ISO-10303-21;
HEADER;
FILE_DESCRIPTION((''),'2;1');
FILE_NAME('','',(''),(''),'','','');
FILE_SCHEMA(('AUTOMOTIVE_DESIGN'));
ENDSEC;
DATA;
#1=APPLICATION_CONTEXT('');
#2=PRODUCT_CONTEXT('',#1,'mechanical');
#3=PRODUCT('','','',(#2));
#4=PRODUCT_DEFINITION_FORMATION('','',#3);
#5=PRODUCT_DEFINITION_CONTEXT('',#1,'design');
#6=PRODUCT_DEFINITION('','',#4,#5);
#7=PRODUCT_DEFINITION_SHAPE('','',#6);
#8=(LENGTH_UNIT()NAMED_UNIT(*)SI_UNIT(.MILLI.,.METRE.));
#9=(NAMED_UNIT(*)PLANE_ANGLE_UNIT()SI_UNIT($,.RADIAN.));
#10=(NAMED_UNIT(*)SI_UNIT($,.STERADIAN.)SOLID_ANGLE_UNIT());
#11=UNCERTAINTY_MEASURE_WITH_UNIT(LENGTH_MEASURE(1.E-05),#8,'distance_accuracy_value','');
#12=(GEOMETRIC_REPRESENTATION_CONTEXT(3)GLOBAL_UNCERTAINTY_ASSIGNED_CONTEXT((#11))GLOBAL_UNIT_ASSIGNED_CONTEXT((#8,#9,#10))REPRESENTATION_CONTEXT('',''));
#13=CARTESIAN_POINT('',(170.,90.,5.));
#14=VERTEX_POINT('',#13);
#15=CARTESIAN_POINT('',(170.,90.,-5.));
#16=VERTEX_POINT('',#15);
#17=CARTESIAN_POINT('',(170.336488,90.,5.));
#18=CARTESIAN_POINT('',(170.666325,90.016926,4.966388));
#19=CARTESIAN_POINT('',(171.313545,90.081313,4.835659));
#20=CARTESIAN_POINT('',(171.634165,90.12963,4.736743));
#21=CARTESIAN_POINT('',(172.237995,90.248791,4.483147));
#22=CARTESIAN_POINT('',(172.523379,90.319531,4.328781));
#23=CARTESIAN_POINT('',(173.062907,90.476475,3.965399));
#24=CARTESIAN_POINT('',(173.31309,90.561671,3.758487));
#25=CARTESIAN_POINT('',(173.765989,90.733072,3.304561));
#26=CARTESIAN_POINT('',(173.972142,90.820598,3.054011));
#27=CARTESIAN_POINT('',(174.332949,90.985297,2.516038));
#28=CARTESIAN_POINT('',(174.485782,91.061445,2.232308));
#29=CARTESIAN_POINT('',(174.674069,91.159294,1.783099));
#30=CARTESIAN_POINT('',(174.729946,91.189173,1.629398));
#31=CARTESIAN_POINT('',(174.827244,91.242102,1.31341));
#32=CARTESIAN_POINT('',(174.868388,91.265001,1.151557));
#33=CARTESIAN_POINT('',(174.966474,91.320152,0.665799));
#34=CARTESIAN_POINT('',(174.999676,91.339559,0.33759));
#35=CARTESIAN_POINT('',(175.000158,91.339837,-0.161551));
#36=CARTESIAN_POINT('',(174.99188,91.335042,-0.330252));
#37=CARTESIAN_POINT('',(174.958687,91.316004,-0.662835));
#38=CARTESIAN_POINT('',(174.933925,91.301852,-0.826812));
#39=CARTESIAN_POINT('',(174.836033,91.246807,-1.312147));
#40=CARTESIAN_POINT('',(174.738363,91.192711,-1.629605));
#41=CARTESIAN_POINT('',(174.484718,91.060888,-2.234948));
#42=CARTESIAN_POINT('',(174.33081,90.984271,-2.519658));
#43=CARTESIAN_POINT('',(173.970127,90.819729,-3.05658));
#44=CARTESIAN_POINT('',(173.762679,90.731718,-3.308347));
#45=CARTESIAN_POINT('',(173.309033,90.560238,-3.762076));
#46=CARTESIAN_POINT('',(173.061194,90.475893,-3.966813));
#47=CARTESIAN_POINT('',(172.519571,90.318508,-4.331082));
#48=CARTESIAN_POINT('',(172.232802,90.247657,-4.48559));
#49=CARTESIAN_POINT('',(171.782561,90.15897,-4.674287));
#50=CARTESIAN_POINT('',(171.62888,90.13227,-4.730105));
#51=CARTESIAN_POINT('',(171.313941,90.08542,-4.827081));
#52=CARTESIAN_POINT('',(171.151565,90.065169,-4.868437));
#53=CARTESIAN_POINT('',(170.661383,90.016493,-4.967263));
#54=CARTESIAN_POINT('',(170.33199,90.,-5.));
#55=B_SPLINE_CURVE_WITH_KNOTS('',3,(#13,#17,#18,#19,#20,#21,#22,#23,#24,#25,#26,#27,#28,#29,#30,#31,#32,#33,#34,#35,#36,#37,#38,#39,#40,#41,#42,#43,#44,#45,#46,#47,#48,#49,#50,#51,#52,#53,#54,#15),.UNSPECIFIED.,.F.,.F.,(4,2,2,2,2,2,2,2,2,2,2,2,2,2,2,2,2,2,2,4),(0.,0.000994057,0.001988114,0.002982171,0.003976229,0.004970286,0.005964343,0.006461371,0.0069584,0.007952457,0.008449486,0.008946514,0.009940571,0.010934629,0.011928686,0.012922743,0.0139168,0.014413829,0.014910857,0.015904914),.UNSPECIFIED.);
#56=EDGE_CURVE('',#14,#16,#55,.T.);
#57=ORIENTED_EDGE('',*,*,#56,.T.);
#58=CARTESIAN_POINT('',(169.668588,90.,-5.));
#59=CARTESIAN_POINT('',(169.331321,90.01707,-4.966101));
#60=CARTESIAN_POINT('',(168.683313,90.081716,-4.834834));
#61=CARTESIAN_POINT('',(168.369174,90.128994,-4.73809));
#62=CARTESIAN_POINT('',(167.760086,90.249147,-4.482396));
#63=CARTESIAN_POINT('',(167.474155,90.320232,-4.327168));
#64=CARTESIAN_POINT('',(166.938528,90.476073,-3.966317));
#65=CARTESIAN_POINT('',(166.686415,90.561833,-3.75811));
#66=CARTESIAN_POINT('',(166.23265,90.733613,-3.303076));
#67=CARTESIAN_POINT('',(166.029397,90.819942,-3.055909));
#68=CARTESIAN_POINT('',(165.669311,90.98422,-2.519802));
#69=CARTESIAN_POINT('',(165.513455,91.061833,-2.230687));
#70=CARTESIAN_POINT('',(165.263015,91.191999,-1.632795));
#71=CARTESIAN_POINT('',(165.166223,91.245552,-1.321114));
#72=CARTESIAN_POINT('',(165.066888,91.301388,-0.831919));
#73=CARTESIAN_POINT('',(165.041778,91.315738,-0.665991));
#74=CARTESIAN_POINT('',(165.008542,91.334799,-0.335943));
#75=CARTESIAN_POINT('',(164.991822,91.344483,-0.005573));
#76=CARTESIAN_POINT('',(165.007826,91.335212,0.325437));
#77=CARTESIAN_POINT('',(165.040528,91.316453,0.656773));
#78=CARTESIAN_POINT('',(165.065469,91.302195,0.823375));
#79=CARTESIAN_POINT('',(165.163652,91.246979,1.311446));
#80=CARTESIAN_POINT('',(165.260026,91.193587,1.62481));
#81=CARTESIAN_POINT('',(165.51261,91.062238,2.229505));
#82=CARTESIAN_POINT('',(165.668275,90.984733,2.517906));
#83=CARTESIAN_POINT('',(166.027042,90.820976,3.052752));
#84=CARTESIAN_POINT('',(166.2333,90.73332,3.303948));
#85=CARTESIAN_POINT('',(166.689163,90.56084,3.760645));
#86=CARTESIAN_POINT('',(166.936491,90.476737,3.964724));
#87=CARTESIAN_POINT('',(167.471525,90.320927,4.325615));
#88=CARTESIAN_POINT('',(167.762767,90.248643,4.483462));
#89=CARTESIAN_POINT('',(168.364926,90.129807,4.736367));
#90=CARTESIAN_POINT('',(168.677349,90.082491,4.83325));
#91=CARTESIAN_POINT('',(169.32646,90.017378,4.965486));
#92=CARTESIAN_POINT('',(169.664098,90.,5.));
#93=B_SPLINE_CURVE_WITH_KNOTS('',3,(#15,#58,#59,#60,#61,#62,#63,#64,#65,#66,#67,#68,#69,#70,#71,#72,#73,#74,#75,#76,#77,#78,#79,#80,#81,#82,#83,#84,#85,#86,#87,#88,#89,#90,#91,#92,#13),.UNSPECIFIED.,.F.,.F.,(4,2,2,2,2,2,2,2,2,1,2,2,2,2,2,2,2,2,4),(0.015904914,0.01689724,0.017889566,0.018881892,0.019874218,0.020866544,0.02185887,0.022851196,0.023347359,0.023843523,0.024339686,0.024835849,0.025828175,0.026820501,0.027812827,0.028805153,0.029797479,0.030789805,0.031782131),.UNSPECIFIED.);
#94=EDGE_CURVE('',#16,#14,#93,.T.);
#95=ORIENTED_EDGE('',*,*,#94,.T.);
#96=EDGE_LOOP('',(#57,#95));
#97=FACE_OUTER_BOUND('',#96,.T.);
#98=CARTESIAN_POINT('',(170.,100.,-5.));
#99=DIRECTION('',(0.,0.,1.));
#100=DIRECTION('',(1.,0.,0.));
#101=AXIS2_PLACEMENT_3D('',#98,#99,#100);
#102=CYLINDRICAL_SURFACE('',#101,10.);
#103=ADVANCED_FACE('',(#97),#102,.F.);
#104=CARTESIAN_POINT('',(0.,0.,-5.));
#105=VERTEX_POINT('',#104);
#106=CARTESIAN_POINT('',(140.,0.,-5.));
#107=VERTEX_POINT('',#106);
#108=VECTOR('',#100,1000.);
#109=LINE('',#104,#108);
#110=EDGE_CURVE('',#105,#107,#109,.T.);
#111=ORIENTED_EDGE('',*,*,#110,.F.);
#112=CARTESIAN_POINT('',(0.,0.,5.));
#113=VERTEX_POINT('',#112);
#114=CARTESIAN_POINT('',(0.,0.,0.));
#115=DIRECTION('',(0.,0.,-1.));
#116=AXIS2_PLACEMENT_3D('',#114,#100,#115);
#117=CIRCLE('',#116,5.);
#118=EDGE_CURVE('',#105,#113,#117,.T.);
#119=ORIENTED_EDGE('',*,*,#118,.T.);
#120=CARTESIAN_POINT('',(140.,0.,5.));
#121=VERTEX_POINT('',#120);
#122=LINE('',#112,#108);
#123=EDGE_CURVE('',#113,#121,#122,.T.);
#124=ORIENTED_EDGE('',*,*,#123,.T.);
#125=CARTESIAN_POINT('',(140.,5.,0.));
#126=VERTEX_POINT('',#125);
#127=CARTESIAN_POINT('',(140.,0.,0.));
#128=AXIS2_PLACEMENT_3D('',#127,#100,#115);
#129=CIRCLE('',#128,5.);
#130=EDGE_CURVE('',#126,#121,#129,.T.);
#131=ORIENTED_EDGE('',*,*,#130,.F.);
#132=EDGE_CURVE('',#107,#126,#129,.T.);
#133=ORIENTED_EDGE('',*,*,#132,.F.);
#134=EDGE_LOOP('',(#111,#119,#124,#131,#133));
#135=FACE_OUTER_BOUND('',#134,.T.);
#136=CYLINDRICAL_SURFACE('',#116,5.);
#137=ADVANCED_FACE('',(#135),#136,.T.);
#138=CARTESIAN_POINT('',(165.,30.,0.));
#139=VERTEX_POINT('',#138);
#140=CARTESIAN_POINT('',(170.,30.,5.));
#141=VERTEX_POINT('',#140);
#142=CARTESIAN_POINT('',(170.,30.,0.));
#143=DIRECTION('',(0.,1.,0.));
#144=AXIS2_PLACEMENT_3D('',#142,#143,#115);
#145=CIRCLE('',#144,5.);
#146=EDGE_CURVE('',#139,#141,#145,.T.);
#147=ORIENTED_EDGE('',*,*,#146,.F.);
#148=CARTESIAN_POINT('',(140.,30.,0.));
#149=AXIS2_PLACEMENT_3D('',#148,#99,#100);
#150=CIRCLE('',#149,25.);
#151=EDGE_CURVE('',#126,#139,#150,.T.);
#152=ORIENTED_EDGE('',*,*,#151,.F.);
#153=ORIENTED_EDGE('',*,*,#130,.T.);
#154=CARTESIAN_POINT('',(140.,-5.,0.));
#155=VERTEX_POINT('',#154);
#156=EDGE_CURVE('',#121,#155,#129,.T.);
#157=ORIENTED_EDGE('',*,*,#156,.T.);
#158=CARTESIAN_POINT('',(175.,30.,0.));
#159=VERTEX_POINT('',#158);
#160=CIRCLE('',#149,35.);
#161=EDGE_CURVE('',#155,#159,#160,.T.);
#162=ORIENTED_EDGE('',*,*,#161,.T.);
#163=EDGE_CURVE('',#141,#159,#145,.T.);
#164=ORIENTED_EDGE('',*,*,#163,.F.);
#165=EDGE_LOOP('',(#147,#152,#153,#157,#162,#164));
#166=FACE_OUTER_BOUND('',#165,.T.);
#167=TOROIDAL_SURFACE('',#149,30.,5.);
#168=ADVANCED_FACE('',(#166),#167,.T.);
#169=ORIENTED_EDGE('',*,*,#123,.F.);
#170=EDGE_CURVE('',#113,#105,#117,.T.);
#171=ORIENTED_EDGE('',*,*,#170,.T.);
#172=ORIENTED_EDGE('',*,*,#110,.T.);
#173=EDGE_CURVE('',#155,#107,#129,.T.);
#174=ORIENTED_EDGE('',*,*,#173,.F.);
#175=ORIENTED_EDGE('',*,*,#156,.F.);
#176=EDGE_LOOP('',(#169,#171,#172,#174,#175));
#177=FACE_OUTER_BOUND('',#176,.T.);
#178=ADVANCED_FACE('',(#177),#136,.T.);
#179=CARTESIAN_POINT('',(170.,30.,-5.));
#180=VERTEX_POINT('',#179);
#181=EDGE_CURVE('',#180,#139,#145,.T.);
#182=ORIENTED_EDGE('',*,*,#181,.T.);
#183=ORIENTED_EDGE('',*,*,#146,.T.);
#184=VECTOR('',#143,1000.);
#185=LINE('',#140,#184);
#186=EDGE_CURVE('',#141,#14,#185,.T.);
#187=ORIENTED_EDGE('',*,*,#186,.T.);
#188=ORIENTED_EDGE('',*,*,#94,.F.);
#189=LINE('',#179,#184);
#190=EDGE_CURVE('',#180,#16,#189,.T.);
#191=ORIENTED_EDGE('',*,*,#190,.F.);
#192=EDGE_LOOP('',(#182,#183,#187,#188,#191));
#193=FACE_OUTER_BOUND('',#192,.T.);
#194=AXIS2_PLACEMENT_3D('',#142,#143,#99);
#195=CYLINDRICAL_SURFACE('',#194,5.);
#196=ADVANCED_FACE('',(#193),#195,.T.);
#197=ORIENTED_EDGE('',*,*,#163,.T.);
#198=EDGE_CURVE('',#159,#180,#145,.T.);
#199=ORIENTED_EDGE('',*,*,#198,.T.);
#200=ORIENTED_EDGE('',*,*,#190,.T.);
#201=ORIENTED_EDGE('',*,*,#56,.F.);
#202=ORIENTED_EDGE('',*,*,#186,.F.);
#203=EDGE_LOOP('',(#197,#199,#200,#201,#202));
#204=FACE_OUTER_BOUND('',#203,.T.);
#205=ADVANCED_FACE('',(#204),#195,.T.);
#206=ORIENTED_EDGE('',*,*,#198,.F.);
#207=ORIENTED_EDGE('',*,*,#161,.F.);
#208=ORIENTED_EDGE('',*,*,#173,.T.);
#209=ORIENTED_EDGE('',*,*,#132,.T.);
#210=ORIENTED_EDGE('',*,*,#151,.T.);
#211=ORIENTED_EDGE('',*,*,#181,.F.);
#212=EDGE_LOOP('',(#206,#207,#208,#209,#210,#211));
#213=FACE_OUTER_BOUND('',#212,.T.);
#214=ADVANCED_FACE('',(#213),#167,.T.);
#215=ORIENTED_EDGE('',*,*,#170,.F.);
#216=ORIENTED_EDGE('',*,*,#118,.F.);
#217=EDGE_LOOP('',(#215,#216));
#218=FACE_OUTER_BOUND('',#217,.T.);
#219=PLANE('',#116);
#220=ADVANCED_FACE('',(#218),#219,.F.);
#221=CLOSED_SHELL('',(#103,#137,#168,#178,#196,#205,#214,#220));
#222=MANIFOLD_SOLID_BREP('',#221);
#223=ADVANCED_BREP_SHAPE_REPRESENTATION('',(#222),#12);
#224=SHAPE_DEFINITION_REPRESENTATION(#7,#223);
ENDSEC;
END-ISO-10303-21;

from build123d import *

# Parameters (mm, degrees)
SKETCH_2_R          = 5
SKETCH_3_R          = 10
CUT_EXTRUDE_1_DEPTH = 5


with BuildPart() as part:
    # 扫描1: sweep along a path in 草图1
    with BuildLine(Plane.XY) as sweep_1_path:
        Line((0, 0), (140, 0))
        ThreePointArc((140, 0), (161.213203436, 8.786796564), (170, 30))
        Line((170, 30), (170, 95))
    # 草图2 → 扫描1 (sweep)
    with BuildSketch(Plane(origin=(0, 0, 0), x_dir=(0, 0, -1), z_dir=(1, 0, 0))):
        Circle(SKETCH_2_R)
    sweep(path=sweep_1_path.line)

    # 草图3 → 切除-拉伸1 (cut, symmetric)
    with BuildSketch(Plane.XY):
        with Locations((170, 100)):
            Circle(SKETCH_3_R)
    extrude(amount=CUT_EXTRUDE_1_DEPTH, both=True, mode=Mode.SUBTRACT)


solid = part.part
